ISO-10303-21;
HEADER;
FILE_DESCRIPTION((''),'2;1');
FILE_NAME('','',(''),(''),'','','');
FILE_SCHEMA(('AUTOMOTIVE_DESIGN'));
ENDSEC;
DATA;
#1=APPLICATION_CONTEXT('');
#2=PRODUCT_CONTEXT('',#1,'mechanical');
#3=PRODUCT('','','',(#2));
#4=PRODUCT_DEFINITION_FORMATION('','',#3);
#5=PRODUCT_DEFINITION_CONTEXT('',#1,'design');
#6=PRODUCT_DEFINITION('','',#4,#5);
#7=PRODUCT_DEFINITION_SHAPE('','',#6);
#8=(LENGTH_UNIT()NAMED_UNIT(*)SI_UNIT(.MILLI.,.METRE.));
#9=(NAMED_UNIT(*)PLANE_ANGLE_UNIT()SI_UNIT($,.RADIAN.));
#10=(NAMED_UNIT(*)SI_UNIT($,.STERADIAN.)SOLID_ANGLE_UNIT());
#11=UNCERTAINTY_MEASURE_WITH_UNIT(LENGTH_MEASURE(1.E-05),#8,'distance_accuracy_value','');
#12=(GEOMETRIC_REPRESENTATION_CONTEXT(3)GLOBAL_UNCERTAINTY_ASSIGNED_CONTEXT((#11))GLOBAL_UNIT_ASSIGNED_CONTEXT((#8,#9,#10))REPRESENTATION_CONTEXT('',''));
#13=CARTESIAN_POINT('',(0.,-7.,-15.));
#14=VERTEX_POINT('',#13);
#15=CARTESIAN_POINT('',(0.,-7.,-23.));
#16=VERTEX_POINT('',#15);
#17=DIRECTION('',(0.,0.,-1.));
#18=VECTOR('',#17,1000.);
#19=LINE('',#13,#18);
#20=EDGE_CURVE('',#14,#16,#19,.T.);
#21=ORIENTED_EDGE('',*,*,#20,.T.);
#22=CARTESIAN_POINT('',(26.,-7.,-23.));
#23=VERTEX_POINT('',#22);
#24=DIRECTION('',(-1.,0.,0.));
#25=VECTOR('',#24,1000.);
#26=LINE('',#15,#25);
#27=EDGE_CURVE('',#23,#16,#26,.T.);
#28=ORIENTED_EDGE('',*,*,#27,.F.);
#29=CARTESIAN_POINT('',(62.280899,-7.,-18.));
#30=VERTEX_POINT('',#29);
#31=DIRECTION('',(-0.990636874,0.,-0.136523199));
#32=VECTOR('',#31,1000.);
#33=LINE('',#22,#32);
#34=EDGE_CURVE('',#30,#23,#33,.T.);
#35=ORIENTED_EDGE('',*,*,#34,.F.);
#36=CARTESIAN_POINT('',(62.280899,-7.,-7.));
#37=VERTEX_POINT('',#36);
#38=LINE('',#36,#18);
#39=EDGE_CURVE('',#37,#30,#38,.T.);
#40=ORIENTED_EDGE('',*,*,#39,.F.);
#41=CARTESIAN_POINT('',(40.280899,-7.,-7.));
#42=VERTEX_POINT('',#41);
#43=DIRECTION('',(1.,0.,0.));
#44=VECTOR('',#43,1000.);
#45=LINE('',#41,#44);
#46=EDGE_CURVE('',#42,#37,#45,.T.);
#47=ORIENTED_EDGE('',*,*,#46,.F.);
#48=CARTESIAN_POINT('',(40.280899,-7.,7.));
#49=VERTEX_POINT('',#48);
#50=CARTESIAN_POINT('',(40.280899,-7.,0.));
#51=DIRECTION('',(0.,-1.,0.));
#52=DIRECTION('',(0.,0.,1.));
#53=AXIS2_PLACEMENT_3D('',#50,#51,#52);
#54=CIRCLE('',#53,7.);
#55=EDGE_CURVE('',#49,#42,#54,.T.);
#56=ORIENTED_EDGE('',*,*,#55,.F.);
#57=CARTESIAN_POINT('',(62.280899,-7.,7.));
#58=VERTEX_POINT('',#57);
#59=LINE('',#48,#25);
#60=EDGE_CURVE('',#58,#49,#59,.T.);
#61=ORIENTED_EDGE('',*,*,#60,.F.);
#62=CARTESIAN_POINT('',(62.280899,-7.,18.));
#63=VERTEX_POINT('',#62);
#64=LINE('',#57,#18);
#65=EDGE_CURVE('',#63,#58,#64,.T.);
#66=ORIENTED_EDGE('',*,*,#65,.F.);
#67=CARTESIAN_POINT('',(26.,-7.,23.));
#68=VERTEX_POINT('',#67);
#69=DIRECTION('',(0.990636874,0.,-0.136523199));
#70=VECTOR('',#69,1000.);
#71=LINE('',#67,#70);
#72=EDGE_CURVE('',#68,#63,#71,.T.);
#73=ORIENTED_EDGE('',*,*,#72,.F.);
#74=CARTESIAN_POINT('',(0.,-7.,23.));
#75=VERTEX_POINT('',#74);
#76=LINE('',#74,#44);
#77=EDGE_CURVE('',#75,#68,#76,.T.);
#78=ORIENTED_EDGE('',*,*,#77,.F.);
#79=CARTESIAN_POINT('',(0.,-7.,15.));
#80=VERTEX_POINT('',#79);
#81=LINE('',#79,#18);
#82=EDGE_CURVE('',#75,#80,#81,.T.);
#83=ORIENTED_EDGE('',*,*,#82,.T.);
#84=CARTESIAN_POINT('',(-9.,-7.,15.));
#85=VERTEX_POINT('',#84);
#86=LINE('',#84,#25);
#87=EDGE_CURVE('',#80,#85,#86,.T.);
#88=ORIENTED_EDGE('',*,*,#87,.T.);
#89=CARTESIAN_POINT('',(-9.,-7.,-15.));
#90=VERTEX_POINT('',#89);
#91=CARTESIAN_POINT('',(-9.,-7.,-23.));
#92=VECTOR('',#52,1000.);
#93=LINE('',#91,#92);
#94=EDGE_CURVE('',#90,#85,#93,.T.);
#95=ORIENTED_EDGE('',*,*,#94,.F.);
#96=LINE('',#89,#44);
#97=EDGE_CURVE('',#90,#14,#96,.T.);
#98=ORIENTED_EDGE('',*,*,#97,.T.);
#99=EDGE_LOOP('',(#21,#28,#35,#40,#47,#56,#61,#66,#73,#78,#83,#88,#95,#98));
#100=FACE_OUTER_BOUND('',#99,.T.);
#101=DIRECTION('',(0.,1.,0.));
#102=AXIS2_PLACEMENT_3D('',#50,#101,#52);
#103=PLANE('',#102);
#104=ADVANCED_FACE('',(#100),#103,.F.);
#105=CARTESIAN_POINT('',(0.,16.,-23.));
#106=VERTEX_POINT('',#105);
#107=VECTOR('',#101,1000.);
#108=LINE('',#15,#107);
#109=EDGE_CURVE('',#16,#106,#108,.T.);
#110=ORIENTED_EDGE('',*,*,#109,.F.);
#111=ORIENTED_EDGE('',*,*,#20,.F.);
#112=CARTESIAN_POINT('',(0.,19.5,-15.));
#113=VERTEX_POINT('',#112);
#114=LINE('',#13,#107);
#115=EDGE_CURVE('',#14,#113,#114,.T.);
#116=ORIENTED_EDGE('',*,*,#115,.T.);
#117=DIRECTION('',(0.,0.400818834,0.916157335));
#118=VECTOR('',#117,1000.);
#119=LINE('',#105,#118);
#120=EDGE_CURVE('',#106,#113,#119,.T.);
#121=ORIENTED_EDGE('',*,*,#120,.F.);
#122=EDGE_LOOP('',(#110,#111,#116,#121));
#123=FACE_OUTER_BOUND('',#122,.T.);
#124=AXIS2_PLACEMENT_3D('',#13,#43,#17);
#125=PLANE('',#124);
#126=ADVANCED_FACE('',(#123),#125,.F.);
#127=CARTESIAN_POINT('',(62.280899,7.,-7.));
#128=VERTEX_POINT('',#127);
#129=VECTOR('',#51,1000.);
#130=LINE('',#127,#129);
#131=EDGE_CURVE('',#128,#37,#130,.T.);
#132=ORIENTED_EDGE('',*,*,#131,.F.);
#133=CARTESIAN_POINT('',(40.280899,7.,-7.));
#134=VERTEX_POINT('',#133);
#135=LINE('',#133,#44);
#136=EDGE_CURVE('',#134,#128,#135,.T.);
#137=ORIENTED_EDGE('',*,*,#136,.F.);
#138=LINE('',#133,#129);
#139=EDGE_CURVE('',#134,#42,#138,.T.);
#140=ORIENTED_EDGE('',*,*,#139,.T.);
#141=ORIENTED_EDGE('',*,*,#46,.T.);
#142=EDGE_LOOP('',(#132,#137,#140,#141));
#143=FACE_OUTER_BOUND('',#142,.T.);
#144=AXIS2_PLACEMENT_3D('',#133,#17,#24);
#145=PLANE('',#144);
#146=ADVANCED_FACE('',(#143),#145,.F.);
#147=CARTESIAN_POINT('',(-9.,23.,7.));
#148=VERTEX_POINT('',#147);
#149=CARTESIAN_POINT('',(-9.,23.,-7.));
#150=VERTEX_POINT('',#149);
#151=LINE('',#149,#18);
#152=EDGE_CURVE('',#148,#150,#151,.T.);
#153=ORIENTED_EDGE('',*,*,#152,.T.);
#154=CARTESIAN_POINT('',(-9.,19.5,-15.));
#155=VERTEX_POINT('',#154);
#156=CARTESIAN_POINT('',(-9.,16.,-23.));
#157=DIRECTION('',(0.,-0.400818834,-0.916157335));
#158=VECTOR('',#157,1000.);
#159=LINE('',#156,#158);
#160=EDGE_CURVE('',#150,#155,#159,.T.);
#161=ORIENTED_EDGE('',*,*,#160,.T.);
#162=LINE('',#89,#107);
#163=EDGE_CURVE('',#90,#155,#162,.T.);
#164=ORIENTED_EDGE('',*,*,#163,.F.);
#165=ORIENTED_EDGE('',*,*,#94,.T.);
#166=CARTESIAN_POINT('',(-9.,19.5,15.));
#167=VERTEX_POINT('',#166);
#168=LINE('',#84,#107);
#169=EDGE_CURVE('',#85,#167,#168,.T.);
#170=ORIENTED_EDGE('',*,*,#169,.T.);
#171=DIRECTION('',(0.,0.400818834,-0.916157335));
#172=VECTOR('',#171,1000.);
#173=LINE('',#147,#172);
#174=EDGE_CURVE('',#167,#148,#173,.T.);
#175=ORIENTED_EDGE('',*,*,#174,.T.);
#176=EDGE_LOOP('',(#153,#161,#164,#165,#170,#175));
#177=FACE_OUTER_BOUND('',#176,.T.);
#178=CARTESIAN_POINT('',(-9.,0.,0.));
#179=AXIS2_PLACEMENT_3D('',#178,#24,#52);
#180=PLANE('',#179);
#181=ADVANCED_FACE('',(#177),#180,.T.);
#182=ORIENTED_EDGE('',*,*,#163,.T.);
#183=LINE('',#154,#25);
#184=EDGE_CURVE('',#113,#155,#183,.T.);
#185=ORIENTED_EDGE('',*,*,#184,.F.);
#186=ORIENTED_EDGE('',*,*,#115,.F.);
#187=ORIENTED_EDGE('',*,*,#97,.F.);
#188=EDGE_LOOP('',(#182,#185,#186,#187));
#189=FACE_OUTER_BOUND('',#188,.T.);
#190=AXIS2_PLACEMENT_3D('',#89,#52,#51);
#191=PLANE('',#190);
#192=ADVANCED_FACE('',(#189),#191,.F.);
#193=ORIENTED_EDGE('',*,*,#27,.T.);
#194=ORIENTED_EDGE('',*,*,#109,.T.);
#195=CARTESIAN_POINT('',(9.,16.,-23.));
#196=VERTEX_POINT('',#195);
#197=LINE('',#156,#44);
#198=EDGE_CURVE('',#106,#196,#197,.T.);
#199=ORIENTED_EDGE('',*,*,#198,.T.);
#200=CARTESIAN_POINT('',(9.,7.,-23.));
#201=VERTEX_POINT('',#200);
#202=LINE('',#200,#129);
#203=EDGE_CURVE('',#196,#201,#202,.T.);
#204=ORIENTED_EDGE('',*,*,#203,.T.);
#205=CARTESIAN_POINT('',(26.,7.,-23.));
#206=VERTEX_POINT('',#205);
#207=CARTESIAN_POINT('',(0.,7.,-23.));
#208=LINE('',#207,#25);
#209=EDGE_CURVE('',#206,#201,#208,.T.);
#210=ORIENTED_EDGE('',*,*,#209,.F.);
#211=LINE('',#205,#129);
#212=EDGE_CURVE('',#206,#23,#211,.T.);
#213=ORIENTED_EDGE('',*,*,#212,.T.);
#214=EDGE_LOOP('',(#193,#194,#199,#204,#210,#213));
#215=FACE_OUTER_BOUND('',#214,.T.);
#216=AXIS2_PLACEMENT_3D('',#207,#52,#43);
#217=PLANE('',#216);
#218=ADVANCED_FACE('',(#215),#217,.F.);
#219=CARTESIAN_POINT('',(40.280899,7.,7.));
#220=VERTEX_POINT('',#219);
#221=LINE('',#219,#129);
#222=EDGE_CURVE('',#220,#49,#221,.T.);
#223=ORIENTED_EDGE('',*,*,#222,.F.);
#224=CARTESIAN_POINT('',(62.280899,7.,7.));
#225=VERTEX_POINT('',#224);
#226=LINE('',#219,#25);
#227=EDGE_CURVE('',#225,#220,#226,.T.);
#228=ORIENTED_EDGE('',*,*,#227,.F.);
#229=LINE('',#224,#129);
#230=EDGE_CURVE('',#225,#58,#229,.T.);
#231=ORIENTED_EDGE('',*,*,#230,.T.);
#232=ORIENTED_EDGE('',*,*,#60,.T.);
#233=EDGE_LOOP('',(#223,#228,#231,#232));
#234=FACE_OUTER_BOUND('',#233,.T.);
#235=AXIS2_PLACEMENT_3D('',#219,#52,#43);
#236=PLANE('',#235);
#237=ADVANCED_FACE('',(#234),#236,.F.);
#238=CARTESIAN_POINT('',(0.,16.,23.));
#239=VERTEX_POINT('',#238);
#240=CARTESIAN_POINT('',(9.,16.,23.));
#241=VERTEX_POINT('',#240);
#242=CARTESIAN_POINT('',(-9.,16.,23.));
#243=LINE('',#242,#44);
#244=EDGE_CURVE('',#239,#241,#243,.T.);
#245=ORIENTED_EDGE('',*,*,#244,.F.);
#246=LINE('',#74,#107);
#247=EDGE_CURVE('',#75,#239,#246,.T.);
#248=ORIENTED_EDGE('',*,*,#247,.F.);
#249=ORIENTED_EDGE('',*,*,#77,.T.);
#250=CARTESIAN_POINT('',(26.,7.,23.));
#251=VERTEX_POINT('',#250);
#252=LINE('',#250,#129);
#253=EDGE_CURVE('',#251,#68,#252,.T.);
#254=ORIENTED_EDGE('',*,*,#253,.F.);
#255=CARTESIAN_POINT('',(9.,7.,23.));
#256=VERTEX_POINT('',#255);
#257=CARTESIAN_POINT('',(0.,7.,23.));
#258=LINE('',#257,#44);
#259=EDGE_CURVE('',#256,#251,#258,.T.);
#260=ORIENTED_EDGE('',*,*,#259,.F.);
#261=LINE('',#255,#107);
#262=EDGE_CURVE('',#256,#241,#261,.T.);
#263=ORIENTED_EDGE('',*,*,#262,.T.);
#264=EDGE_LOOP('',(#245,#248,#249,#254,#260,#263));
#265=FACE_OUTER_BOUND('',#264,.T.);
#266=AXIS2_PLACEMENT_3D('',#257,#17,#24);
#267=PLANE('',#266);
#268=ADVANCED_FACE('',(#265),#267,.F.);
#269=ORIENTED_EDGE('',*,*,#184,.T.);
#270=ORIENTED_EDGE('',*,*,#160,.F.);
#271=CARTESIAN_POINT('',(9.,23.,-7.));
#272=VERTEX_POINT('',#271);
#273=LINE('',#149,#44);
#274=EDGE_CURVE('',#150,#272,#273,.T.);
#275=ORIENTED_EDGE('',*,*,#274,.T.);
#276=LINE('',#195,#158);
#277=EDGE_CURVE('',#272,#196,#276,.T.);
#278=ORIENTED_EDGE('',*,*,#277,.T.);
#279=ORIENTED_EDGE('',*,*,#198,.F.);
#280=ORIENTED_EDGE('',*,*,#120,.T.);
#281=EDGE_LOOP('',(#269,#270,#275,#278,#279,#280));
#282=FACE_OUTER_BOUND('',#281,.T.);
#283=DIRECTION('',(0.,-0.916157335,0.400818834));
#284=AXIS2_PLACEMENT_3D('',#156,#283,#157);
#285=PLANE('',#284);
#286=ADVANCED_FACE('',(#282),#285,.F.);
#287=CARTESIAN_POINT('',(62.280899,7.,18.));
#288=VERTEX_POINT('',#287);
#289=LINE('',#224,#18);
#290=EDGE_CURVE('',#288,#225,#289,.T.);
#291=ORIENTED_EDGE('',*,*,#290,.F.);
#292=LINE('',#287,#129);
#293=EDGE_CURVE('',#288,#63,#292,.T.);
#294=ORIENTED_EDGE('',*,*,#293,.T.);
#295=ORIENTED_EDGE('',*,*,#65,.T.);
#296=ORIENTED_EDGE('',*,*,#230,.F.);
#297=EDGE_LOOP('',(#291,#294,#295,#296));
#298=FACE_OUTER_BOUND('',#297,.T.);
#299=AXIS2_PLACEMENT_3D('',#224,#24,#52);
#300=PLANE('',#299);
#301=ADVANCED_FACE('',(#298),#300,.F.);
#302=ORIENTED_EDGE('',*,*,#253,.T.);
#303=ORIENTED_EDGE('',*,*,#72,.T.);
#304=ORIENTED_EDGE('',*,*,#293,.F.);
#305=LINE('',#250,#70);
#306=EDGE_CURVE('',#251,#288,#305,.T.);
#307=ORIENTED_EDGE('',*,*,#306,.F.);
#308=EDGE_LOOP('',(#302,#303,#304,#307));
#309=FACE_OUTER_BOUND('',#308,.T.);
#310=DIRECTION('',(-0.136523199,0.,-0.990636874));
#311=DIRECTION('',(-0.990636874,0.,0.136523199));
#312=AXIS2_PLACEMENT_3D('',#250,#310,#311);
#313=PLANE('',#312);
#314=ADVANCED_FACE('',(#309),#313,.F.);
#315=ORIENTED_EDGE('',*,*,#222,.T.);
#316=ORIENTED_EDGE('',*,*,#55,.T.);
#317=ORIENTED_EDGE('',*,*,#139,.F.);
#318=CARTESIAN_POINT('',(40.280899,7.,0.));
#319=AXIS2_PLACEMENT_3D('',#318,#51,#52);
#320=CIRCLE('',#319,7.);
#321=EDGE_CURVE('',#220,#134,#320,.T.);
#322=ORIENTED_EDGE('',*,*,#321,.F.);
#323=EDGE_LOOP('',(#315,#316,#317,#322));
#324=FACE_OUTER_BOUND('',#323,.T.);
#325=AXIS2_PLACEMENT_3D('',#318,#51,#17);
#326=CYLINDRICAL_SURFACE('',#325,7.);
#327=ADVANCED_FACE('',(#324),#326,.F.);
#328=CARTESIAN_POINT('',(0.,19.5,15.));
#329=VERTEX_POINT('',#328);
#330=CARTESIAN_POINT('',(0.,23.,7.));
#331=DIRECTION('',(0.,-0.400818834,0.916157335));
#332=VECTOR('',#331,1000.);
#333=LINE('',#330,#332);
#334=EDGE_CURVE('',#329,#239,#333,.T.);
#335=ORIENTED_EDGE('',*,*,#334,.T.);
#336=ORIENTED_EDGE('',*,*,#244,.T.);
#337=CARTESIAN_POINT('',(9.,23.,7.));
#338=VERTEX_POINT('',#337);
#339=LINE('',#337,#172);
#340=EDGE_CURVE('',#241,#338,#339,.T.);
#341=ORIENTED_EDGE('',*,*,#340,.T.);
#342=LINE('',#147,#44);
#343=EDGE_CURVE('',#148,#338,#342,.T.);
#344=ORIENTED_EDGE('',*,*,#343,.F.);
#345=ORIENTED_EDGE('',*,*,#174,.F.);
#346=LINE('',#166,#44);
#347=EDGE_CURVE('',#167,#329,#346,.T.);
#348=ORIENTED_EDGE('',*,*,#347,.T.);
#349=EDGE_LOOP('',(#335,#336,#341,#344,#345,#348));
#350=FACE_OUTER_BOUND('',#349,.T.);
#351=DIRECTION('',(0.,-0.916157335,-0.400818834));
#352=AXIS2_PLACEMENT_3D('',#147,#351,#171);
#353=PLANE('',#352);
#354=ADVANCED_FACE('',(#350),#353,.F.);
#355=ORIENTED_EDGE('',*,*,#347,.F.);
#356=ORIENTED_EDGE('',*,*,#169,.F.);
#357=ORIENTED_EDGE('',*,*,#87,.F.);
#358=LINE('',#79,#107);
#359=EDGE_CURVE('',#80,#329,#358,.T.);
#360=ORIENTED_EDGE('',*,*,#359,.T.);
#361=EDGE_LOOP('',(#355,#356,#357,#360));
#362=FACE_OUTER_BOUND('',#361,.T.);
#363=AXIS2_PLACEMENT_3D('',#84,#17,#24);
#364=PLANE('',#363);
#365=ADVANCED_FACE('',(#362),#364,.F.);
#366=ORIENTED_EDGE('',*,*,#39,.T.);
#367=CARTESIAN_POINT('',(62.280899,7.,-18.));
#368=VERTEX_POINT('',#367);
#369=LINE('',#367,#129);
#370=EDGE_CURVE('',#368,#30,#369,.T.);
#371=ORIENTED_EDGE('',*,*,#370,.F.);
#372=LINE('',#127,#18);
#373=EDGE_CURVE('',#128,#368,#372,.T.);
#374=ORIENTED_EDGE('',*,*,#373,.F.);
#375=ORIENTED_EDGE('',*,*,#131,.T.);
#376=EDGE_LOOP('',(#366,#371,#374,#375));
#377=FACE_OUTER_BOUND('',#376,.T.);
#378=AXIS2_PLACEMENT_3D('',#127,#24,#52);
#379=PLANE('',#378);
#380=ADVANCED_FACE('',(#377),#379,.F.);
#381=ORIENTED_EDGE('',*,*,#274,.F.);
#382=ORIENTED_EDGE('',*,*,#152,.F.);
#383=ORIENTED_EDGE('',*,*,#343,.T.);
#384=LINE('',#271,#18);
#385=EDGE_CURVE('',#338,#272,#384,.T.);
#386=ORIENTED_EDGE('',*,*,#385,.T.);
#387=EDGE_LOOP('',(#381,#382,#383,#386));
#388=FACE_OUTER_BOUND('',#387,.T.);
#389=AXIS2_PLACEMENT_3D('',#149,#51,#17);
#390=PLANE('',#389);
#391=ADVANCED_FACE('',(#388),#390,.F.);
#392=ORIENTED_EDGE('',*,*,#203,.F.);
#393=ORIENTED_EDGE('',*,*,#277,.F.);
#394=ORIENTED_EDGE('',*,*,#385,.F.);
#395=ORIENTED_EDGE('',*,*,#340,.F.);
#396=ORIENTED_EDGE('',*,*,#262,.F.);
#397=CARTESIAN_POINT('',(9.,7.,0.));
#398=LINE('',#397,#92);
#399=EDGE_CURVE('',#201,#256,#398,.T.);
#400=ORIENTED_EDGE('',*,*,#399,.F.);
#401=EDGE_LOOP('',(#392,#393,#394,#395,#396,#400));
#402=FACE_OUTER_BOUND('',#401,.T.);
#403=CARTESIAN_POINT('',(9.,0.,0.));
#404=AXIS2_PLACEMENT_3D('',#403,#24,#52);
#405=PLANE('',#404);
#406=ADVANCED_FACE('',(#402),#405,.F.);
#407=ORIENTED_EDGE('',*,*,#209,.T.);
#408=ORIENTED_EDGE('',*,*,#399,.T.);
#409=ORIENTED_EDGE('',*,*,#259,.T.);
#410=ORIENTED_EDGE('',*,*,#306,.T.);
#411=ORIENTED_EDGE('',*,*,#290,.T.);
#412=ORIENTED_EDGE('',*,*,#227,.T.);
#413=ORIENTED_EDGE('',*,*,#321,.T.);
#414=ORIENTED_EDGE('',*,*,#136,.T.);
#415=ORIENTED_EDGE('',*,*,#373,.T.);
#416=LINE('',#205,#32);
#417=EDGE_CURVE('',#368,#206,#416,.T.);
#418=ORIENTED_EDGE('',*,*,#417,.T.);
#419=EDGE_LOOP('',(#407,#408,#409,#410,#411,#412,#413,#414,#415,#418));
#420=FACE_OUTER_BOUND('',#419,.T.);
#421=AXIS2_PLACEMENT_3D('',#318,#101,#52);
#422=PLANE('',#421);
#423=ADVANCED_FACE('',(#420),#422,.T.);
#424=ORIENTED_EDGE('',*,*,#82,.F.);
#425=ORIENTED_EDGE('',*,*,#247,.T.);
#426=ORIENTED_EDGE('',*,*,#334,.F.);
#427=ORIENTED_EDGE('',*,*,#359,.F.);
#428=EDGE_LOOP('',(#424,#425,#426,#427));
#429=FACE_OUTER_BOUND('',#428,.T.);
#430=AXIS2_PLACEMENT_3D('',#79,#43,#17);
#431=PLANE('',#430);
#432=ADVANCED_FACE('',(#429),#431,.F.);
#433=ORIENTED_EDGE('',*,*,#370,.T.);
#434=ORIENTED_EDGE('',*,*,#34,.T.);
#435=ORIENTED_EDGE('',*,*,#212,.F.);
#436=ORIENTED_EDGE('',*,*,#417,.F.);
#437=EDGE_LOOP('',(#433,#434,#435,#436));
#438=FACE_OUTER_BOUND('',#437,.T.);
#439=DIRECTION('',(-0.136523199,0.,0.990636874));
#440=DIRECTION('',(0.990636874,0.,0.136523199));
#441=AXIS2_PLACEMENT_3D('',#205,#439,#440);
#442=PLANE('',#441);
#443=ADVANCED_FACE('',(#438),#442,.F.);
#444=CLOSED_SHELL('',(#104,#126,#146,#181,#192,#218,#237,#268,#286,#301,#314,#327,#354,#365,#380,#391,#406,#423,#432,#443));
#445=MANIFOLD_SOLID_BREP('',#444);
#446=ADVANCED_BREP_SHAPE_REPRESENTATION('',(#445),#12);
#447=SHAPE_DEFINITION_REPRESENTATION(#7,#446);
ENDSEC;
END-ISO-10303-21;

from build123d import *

# Parameters (mm, degrees)
BASE_PLATE_14MM_WITH_U_SLOT_DEPTH = 7
RAISED_BLOCK_18MM_DEPTH           = 9
STEP_CUT_SKETCH_W                 = 9
STEP_CUT_SKETCH_H                 = 8
STEP_CUT_DEPTH                    = 73.855407245


with BuildPart() as part:
    # Base Plate Profile Sketch → Base Plate 14mm with U-Slot (new, symmetric)
    with BuildSketch(Plane(origin=(0, 0, 0), x_dir=(1, 0, 0), z_dir=(0, 1, 0))):
        with BuildLine():
            Line((0, 23), (0, -23))
            Line((0, -23), (26, -23))
            Line((26, -23), (62.280898876, -18))
            Line((62.280898876, -18), (62.280898876, -7))
            Line((62.280898876, -7), (40.280898876, -7))
            ThreePointArc((40.280898876, -7), (33.280898876, 0), (40.280898876, 7))
            Line((40.280898876, 7), (62.280898876, 7))
            Line((62.280898876, 7), (62.280898876, 18))
            Line((62.280898876, 18), (26, 23))
            Line((26, 23), (0, 23))
        make_face()
    extrude(amount=BASE_PLATE_14MM_WITH_U_SLOT_DEPTH, both=True)

    # Raised Block Sketch → Raised Block 18mm (add, symmetric)
    with BuildSketch(Plane.ZY):
        Polygon((-23, 7), (-23, 16), (-7, 23), (7, 23), (23, 16), (23, 7), (23, -7), (-23, -7), align=None)
    extrude(amount=RAISED_BLOCK_18MM_DEPTH, both=True)

    # Step Cut Sketch → Step Cut (cut, through all)
    with BuildSketch(Plane(origin=(0, 23, 0), x_dir=(1, 0, 0), z_dir=(0, 1, 0))):
        with Locations((-4.5, 19)):
            Rectangle(STEP_CUT_SKETCH_W, STEP_CUT_SKETCH_H)
        with Locations((-4.5, -19)):
            Rectangle(STEP_CUT_SKETCH_W, STEP_CUT_SKETCH_H)
    extrude(amount=-STEP_CUT_DEPTH, mode=Mode.SUBTRACT)


solid = part.part
